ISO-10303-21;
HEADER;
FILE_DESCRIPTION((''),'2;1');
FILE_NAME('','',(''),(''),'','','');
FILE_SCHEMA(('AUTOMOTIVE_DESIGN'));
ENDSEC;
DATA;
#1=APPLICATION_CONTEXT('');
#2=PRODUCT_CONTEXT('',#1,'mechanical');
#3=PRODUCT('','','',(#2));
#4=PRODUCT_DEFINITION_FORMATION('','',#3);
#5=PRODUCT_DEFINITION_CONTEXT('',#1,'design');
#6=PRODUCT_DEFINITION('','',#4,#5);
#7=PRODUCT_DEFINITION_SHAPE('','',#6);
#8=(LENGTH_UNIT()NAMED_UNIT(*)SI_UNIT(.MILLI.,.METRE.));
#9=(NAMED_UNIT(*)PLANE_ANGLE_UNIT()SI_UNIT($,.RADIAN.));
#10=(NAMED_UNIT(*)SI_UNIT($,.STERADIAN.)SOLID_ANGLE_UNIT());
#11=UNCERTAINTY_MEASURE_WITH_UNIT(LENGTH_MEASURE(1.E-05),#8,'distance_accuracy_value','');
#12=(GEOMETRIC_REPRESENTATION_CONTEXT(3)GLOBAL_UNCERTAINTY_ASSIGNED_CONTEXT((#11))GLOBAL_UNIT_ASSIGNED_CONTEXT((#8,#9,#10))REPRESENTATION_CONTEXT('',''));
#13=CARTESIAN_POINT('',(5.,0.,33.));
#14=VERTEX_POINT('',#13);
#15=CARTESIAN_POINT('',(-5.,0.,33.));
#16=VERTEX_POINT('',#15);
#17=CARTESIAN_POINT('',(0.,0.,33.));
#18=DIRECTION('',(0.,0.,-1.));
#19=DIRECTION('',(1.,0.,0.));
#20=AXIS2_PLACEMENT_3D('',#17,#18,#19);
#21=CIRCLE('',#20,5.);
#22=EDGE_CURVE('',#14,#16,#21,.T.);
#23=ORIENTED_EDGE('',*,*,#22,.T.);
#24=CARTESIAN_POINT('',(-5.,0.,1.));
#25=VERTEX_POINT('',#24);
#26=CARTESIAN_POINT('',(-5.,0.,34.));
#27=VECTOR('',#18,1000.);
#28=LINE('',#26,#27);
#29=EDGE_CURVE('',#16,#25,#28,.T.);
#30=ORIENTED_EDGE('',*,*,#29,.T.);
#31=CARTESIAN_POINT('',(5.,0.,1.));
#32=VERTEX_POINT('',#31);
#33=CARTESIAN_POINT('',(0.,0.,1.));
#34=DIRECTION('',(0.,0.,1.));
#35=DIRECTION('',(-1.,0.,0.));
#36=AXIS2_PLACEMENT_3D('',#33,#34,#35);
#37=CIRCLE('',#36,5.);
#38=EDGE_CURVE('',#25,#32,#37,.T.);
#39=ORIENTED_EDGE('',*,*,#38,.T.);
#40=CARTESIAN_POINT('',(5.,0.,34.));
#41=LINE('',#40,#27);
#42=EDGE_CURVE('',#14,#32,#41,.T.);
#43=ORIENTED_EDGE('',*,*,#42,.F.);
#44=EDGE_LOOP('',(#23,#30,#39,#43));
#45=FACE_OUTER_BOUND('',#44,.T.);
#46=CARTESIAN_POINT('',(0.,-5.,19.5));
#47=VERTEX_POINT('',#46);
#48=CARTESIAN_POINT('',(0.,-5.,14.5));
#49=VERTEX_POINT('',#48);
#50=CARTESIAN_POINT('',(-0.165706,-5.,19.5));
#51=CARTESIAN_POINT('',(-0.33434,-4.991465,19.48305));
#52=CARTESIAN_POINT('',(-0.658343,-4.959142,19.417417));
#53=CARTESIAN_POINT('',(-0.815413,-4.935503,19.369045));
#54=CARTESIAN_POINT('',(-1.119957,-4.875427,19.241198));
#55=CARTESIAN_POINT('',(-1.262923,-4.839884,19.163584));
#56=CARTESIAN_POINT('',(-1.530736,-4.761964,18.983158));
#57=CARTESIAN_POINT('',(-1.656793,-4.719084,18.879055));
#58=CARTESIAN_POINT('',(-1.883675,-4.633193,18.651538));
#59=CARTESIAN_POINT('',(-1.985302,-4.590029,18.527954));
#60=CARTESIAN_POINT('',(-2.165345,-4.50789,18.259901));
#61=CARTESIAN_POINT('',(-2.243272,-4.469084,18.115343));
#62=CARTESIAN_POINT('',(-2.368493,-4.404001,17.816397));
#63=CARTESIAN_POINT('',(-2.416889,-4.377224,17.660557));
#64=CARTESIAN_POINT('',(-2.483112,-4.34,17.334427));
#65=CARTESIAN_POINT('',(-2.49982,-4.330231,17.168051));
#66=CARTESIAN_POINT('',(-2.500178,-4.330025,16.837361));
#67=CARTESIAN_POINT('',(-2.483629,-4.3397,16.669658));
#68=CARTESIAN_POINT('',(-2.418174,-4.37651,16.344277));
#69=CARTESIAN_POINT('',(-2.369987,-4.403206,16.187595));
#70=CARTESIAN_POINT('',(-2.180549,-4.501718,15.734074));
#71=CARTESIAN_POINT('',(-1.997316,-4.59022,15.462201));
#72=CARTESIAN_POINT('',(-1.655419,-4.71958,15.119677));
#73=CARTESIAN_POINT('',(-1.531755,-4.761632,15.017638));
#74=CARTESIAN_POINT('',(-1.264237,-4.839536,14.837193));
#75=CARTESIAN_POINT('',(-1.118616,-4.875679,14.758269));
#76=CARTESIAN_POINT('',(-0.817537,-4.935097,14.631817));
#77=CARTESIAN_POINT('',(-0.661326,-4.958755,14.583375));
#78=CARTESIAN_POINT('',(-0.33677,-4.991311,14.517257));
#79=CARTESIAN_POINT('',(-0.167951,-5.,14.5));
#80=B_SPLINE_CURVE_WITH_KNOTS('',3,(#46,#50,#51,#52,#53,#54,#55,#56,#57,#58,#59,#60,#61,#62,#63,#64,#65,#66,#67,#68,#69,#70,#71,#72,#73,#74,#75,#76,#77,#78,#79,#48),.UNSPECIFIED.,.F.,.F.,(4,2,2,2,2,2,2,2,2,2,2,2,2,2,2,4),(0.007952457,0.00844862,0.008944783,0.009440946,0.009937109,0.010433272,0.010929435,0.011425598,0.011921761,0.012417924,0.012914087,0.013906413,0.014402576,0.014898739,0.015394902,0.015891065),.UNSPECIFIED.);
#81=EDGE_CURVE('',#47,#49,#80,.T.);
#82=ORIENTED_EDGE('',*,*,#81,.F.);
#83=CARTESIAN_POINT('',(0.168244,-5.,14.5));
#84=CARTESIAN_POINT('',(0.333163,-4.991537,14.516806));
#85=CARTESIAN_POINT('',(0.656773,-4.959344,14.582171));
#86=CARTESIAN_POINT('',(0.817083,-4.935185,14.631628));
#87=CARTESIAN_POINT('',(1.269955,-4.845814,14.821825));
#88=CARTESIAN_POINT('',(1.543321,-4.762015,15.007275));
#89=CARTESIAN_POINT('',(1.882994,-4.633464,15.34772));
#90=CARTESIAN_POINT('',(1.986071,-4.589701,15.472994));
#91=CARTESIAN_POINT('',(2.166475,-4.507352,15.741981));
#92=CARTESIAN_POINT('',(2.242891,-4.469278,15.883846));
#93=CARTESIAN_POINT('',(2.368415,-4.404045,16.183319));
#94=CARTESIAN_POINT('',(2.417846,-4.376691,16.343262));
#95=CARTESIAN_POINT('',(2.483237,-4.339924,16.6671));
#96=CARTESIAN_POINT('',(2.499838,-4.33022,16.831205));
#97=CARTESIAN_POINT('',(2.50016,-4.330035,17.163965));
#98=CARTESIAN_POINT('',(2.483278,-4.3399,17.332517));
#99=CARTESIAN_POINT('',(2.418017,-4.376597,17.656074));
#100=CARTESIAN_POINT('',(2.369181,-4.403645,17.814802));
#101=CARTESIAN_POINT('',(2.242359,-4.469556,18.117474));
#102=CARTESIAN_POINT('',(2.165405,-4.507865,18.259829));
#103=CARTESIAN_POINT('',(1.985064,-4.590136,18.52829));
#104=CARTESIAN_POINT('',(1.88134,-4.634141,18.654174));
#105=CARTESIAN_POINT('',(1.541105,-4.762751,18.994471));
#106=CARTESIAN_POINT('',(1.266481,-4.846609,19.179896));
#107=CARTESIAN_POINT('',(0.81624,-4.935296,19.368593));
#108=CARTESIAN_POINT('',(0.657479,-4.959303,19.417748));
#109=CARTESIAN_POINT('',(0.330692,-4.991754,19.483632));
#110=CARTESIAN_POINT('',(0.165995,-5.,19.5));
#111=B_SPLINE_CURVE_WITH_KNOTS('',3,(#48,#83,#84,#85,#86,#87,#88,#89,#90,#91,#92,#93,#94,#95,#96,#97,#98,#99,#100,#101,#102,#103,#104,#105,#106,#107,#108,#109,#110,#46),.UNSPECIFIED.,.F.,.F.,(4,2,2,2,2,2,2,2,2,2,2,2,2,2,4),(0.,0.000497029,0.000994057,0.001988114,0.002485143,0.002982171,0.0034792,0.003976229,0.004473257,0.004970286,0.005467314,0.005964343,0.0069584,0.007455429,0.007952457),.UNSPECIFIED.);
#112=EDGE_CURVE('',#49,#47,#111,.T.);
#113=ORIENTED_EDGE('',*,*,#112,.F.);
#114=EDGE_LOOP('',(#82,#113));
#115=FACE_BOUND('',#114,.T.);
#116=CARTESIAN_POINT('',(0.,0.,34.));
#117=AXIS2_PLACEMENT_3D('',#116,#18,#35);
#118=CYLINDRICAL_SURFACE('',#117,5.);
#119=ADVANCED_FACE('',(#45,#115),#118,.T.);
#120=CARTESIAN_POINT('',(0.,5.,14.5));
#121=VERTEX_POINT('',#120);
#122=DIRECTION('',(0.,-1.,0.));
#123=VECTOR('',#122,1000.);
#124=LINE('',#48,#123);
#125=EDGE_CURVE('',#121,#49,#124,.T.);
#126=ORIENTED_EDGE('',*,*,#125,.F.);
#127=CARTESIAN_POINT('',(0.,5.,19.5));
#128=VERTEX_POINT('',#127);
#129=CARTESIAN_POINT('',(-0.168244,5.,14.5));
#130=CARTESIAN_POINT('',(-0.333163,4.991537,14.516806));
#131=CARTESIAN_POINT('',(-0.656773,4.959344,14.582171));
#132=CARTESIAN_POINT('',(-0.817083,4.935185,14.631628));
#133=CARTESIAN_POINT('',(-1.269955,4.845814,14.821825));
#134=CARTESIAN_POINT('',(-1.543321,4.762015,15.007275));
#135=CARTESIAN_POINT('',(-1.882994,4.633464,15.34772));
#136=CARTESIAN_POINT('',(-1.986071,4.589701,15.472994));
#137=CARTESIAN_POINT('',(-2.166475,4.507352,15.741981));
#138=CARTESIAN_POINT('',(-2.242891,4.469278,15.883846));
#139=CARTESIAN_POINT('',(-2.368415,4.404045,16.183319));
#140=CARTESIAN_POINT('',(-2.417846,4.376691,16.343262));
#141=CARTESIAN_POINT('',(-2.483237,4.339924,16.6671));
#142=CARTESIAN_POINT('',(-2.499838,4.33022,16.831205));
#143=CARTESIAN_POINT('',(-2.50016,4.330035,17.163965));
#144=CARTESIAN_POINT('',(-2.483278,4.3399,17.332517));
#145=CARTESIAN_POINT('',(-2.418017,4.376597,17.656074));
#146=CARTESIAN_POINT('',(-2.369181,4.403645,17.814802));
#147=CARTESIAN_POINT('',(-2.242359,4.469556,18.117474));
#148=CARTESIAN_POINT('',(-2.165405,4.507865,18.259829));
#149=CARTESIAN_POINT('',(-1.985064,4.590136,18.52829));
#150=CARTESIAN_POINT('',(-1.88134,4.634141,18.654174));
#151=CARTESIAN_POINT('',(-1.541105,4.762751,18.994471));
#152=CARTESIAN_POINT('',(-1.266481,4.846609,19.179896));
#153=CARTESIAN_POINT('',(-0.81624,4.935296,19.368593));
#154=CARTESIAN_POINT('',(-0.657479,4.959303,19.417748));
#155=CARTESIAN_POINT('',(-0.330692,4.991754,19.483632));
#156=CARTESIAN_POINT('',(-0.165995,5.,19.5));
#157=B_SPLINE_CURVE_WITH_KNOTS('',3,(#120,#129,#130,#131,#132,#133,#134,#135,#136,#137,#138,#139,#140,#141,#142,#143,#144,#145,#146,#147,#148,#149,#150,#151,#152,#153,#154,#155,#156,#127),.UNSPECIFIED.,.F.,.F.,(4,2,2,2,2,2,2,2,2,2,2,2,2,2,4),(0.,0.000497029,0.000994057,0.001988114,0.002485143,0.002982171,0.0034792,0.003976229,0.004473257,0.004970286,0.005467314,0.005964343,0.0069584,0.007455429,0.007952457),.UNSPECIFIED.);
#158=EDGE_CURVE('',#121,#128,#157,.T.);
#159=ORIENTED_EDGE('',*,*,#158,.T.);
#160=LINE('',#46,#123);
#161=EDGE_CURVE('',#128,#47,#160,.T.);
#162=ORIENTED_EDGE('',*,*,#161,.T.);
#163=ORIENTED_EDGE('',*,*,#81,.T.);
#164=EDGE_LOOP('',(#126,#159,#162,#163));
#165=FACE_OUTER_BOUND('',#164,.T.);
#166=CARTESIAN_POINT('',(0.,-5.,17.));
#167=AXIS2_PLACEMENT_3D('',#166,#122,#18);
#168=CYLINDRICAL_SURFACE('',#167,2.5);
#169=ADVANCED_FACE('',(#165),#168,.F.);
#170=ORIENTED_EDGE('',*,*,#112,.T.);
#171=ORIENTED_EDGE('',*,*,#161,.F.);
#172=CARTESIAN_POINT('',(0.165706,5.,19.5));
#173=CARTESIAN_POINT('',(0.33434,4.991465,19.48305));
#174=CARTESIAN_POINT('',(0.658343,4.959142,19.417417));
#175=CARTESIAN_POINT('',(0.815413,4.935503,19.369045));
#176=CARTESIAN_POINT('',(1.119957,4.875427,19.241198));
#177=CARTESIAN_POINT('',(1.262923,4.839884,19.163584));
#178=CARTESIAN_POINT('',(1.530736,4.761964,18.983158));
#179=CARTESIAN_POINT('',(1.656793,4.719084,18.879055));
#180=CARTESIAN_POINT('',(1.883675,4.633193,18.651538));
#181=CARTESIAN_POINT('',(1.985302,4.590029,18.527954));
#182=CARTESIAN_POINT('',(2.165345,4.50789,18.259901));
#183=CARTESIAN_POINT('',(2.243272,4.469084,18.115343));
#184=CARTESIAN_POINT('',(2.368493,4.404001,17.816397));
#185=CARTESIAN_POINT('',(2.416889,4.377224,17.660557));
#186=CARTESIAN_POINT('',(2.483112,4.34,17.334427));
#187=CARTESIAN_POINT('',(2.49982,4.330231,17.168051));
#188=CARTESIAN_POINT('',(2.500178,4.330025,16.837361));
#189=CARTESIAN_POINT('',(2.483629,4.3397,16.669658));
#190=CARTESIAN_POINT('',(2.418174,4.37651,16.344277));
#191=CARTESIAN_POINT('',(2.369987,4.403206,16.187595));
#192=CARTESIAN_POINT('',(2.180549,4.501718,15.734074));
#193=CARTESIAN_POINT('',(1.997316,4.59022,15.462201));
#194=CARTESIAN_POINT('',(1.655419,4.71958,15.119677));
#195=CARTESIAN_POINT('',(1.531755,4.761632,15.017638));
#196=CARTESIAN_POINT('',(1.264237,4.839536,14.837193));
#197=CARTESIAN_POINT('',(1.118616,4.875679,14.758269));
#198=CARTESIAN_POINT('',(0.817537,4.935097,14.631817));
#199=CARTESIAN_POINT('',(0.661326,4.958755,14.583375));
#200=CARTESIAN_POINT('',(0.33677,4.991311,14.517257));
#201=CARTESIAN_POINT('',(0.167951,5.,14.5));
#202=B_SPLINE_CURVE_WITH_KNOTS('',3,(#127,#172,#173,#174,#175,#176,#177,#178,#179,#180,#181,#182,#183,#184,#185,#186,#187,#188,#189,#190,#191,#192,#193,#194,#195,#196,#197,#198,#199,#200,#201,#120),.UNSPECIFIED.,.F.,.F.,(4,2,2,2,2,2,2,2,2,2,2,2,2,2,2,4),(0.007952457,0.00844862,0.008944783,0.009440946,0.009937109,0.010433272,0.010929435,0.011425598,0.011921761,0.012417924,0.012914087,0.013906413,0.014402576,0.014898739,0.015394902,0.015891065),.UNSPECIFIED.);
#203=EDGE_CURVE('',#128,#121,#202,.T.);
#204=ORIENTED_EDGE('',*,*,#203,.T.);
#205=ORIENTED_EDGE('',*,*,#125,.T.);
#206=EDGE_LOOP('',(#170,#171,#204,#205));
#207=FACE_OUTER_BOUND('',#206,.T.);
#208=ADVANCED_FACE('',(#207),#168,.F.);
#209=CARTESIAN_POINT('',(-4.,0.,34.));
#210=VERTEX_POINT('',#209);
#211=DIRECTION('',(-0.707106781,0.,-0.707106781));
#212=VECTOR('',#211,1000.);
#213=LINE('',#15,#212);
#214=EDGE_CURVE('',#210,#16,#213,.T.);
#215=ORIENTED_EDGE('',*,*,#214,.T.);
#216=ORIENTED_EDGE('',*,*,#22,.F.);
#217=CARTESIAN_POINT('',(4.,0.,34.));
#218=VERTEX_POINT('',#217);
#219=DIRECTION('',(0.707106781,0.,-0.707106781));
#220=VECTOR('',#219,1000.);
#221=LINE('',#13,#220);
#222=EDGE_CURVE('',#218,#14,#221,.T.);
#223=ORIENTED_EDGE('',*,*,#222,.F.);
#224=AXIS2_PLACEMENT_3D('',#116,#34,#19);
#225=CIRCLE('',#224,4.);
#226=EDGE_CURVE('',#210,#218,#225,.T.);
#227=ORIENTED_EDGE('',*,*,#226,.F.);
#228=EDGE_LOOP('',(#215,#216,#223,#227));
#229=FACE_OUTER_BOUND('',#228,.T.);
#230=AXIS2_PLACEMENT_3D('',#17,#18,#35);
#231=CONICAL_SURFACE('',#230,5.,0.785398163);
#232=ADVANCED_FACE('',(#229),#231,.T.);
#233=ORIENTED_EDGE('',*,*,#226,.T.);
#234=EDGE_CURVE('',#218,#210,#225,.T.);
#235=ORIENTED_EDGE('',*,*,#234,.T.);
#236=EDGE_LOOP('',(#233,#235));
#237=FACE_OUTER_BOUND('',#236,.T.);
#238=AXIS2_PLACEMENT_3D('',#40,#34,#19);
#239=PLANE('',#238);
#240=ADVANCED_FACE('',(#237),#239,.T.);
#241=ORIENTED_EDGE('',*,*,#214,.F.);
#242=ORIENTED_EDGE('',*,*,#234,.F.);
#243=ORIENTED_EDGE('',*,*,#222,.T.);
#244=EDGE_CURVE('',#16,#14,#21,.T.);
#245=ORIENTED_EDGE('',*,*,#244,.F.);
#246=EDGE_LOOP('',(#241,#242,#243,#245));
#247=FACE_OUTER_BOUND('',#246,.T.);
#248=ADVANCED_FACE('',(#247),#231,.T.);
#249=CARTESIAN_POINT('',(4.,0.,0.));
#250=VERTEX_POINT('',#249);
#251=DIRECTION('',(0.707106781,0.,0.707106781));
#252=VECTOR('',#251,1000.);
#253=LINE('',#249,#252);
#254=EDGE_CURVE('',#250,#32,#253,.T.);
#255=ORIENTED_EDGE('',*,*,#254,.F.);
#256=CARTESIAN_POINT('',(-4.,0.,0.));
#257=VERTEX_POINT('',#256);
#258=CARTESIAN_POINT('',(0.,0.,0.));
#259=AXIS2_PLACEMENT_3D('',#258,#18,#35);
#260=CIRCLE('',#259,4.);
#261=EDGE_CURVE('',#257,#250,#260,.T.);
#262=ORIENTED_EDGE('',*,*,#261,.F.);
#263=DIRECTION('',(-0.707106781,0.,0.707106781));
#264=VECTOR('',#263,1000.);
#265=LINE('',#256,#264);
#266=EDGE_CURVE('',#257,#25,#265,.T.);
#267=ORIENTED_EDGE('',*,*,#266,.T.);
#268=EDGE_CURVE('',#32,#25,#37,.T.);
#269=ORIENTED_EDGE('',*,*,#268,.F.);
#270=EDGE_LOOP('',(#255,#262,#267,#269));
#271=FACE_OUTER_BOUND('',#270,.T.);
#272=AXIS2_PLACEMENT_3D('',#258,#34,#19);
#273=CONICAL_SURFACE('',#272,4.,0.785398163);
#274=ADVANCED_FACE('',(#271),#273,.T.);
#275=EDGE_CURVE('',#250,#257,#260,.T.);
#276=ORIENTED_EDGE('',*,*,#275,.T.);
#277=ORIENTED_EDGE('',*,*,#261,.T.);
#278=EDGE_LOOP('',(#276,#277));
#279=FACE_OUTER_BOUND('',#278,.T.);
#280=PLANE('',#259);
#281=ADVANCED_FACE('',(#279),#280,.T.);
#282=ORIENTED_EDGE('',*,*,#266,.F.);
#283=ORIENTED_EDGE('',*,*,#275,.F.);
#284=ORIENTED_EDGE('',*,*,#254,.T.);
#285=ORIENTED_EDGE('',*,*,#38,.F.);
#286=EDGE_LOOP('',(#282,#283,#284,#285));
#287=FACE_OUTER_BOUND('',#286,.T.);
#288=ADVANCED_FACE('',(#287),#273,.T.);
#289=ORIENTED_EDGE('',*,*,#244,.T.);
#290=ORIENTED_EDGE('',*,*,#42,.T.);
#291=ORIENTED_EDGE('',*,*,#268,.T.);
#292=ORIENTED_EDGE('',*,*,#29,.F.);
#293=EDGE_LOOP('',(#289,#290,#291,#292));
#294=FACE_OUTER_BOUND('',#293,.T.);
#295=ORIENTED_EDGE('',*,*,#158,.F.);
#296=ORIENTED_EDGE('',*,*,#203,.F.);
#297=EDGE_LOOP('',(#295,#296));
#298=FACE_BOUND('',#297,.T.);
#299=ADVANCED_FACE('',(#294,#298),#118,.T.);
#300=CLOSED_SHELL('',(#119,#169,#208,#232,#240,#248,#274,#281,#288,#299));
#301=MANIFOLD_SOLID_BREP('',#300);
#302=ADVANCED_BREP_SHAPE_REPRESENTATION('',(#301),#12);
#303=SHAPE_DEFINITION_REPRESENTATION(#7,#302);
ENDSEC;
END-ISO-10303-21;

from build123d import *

# Parameters (mm, degrees)
SKETCH1_W                = 5
SKETCH1_H                = 34
F_5_0_5_DIAMETER_HOLE1_D = 5
CHAMFER1_SIZE            = 1


with BuildPart() as part:
    # Sketch1 → Revolve1 (revolve)
    with BuildSketch(Plane.XZ, mode=Mode.PRIVATE) as revolve1_sk:
        with Locations((2.5, 17)):
            Rectangle(SKETCH1_W, SKETCH1_H)
    revolve(revolve1_sk.sketch.rotate(Axis((0, 0, 34), (0, 0, -1)), 180), axis=Axis((0, 0, 34), (0, 0, -1)))

    # Ø5.0 (5) Diameter Hole1 (through all)
    with Locations(Plane(origin=(0, -5, 17), x_dir=(-1, 0, 0), z_dir=(0, -1, 0))):
        with Locations((0, 0)):
            Hole(F_5_0_5_DIAMETER_HOLE1_D / 2)

    # Chamfer1
    chamfer1_edges = [part.edges().sort_by_distance(p)[0] for p in [
        (5, 0, 0),
        (5, 0, 34),
    ]]
    chamfer(chamfer1_edges, length=CHAMFER1_SIZE)


solid = part.part
